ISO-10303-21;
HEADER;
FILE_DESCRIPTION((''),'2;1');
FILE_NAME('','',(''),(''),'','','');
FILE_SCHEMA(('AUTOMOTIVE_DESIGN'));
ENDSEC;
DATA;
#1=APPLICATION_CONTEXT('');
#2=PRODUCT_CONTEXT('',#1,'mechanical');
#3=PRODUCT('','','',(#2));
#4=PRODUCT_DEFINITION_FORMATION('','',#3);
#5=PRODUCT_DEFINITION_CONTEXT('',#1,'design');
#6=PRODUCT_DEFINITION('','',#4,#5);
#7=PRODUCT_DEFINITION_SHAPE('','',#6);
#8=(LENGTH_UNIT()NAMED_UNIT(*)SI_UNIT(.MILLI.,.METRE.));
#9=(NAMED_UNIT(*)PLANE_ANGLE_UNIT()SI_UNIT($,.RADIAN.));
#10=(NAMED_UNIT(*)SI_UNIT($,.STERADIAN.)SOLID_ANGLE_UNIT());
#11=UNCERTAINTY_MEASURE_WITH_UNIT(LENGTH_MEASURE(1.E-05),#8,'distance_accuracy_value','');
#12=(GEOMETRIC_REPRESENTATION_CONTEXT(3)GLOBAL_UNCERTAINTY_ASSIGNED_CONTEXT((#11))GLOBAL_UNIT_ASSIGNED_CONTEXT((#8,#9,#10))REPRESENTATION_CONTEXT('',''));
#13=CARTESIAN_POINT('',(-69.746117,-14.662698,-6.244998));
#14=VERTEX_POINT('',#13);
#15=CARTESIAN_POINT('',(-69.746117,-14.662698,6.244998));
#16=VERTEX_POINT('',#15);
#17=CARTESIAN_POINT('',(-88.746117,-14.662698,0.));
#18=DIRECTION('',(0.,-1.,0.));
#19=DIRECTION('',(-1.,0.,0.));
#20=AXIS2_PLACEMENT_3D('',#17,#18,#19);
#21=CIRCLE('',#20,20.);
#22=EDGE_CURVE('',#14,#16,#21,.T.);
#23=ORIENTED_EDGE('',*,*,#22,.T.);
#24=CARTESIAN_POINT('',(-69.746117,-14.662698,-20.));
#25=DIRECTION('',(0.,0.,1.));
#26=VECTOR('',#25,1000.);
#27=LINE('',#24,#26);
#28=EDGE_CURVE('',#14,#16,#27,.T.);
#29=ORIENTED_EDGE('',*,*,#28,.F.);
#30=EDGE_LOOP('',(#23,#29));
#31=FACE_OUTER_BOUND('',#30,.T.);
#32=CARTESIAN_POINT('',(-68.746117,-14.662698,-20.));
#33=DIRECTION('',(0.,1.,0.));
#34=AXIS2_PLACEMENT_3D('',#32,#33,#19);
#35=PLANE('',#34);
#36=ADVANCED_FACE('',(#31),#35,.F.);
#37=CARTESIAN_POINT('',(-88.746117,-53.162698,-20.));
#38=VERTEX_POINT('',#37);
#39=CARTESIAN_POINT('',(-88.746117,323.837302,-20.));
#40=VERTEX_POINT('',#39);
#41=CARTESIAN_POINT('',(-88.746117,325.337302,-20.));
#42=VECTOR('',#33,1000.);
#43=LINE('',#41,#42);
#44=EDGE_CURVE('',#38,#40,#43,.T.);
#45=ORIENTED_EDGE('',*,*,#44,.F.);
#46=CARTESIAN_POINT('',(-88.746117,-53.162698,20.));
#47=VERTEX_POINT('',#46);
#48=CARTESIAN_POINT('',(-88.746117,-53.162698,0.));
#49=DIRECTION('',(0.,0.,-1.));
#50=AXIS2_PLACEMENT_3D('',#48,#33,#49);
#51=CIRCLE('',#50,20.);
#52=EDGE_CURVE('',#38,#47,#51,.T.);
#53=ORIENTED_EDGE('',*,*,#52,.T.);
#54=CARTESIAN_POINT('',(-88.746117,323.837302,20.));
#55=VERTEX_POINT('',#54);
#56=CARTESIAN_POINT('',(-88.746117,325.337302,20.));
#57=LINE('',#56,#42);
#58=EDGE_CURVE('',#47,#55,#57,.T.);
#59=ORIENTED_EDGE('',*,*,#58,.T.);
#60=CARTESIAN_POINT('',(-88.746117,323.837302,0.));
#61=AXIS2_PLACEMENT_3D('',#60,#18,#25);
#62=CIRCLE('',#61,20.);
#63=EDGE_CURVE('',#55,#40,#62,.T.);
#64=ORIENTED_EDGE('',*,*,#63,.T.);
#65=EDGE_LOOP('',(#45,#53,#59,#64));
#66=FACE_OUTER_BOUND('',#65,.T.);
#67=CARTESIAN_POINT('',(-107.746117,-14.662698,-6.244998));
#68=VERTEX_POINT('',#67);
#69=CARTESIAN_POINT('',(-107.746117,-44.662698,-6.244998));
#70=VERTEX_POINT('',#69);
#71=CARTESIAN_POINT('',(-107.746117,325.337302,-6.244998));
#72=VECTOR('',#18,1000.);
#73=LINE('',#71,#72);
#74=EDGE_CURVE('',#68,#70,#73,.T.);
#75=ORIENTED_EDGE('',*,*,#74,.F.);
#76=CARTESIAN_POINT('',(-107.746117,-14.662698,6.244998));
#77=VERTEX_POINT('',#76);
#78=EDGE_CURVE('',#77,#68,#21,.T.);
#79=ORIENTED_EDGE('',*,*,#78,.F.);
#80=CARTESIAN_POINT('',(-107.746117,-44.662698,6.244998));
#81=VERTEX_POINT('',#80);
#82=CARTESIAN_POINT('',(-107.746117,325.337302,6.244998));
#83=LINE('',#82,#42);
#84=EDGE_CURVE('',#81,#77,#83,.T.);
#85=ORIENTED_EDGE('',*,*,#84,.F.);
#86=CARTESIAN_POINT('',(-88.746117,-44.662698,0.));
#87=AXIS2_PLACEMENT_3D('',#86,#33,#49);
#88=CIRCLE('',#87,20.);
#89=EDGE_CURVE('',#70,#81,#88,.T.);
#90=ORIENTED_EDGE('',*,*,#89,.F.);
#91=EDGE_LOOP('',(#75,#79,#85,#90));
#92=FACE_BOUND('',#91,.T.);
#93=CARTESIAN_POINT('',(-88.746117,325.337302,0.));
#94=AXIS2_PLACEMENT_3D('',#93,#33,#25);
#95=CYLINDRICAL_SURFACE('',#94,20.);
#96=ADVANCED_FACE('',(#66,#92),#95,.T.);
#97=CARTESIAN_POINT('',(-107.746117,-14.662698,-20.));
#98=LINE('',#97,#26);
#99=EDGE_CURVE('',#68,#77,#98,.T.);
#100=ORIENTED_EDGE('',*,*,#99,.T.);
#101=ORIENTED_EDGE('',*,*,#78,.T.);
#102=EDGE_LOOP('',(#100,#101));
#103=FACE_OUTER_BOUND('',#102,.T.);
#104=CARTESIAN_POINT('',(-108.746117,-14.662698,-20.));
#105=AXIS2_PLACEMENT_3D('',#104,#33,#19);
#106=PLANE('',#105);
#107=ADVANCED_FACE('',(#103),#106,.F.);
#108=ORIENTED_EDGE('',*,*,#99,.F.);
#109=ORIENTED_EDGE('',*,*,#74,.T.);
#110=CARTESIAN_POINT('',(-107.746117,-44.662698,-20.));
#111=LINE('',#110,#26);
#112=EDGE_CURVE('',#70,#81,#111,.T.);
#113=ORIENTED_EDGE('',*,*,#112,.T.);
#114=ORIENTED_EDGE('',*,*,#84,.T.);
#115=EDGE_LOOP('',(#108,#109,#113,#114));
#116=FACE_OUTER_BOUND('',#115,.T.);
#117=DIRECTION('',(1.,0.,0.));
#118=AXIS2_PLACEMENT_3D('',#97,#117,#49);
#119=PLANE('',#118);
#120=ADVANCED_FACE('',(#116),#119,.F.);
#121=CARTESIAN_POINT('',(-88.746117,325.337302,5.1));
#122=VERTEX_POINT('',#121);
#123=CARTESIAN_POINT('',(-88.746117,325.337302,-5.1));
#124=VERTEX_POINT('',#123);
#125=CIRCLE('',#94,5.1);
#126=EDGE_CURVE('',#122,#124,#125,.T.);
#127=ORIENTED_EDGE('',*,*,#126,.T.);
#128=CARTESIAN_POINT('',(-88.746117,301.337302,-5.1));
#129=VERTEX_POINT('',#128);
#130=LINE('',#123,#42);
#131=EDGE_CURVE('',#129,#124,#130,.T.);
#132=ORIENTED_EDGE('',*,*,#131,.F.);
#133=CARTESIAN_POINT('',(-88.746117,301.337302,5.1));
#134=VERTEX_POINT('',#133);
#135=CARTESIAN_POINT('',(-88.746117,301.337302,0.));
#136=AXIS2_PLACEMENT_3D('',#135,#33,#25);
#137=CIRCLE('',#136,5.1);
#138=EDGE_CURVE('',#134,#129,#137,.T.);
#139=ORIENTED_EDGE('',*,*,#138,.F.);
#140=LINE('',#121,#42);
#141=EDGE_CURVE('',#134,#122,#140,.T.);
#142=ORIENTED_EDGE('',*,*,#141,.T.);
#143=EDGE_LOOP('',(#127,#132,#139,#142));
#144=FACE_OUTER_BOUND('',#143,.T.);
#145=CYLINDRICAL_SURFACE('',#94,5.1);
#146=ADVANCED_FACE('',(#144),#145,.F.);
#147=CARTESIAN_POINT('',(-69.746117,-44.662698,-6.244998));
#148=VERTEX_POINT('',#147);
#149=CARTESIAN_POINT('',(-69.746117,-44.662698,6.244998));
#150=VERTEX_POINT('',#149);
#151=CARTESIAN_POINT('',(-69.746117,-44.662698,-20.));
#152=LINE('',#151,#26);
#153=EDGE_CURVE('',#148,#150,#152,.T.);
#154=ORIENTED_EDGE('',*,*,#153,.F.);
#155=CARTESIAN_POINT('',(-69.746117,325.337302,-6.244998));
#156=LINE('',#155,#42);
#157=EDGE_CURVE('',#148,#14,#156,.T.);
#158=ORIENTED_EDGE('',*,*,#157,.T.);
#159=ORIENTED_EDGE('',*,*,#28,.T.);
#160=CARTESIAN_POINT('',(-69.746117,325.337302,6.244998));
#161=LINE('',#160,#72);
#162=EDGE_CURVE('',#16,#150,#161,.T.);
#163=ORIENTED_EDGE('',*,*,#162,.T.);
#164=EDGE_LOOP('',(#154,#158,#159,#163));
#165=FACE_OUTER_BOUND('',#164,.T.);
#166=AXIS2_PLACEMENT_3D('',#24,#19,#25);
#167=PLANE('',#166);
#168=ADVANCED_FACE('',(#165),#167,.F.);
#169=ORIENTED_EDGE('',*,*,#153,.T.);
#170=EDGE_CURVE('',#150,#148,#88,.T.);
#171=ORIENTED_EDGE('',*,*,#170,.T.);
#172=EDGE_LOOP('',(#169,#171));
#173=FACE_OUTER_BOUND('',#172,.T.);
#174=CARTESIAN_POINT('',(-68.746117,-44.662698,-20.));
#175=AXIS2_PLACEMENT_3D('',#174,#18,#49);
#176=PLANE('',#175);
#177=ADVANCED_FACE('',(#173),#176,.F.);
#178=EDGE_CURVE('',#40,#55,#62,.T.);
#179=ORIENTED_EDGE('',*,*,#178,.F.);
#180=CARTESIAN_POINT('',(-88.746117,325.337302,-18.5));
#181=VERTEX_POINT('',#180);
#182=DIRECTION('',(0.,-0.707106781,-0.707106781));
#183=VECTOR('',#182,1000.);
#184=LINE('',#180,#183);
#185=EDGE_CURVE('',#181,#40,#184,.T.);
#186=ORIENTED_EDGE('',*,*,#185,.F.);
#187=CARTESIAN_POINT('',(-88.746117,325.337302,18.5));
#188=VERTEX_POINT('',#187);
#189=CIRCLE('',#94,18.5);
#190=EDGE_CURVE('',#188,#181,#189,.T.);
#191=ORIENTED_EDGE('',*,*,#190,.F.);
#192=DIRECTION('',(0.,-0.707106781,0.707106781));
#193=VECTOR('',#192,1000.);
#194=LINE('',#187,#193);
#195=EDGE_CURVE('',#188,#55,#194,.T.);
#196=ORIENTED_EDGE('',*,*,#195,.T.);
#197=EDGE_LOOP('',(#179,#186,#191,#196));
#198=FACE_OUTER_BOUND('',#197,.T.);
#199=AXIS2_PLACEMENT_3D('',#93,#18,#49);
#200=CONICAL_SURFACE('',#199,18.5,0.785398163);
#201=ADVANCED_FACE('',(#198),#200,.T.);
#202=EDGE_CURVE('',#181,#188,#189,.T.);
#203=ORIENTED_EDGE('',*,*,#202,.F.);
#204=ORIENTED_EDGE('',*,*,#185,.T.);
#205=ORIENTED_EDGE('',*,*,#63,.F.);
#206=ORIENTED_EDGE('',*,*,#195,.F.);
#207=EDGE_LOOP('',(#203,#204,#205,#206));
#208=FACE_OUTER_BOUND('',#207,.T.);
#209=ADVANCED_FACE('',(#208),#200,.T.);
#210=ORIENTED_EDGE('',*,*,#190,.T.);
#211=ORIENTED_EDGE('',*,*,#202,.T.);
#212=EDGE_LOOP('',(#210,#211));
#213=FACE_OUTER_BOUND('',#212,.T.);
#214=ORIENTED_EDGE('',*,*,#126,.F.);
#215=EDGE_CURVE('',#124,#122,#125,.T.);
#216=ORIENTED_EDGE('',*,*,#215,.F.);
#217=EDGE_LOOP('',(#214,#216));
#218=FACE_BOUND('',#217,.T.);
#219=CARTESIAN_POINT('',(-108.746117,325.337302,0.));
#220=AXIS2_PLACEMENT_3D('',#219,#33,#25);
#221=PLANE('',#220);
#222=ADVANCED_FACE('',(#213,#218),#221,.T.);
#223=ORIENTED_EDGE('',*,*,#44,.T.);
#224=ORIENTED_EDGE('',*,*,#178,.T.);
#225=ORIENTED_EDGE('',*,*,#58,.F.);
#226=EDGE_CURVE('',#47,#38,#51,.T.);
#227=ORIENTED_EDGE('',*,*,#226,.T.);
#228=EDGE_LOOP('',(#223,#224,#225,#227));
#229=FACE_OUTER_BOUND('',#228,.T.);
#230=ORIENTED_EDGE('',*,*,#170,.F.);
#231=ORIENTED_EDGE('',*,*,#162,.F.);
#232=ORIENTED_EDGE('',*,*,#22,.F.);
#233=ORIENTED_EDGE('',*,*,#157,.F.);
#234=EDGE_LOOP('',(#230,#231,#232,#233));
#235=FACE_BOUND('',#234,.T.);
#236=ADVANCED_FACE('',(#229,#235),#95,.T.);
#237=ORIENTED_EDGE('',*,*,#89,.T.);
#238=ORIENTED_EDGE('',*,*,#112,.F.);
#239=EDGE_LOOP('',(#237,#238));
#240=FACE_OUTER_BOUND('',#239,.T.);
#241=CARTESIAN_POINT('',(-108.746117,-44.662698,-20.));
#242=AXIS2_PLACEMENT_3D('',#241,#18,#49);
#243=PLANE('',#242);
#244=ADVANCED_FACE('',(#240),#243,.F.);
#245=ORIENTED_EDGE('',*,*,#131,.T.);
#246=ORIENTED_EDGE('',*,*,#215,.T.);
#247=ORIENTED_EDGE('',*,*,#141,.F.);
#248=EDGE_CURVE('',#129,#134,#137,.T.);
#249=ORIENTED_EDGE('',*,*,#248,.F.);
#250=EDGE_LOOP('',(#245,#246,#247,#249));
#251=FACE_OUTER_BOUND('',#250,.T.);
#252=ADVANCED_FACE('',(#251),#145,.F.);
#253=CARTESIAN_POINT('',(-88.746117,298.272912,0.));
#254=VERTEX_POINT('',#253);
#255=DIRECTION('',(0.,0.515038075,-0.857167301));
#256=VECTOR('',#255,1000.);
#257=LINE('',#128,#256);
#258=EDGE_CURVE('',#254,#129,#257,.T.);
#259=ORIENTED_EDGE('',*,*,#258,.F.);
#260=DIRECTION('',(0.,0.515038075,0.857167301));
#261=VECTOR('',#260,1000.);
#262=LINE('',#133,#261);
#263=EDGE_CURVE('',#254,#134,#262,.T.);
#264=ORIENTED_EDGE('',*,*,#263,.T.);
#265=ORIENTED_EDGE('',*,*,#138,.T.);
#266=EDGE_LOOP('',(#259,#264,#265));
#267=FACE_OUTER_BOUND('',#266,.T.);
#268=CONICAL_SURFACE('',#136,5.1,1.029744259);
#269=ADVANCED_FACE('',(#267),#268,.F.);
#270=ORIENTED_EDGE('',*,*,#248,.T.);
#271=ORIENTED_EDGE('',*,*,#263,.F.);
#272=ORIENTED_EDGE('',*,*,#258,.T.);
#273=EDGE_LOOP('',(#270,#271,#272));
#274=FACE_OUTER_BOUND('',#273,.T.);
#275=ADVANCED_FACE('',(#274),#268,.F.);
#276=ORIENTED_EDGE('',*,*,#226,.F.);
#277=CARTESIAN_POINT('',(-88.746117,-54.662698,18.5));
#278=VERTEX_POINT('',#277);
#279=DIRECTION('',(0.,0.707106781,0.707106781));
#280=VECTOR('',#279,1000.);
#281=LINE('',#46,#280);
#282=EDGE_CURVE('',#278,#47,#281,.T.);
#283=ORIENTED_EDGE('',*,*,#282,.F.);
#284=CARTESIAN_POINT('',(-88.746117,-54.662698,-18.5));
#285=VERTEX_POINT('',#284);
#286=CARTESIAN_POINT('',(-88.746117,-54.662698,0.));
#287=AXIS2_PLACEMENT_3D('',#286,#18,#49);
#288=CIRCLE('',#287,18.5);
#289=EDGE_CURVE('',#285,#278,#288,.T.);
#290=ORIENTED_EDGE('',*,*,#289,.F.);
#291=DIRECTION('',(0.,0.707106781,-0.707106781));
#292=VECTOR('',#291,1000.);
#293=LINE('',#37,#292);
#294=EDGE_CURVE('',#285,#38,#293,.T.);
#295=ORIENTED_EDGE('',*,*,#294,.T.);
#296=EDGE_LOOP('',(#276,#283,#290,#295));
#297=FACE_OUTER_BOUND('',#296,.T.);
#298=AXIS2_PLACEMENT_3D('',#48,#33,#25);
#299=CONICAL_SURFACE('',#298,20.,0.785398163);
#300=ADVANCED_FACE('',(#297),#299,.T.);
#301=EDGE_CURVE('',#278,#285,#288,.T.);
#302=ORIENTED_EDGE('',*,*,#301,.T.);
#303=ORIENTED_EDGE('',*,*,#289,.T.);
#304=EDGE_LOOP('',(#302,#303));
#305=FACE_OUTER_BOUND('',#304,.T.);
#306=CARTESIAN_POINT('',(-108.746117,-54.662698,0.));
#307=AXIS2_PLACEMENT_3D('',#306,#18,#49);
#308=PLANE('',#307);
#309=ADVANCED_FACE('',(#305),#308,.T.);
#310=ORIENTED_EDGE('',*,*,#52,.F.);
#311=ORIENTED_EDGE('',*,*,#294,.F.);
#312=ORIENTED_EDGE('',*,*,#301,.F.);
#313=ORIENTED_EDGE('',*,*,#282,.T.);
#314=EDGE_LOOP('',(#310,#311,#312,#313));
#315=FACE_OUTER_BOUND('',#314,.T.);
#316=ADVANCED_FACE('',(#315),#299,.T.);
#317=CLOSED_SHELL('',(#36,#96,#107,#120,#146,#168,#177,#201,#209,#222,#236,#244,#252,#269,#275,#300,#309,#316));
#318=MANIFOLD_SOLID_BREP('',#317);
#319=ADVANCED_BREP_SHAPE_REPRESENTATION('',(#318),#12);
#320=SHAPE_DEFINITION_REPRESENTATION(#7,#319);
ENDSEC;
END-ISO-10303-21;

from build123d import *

# Parameters (mm, degrees)
SKETCH1_W               = 20
SKETCH1_H               = 380
CUT_EXTRUDE1_DEPTH      = 344.613267812
CUT_EXTRUDE1_DEPTH_BACK = 344.613267812
SKETCH2_W               = 1
SKETCH2_H               = 30
CHAMFER1_SIZE           = 1.5
M12_TAPPED_HOLE1_D      = 10.2
M12_TAPPED_HOLE1_DEPTH  = 24
M12_TAPPED_HOLE1_TIP    = 3.064389157


with BuildPart() as part:
    # Sketch1 → Revolve1 (revolve)
    with BuildSketch(Plane.XY, mode=Mode.PRIVATE) as revolve1_sk:
        with Locations((-98.74611723, 135.337301587)):
            Rectangle(SKETCH1_W, SKETCH1_H)
    revolve(revolve1_sk.sketch.rotate(Axis((-88.74611723, 325.337301587, 0), (0, -1, 0)), 270), axis=Axis((-88.74611723, 325.337301587, 0), (0, -1, 0)))

    # Sketch2 → Cut-Extrude1 (cut, two sides: drawn at the far end of the back side and taken through both)
    with BuildSketch(Plane.XY.offset(-CUT_EXTRUDE1_DEPTH_BACK)):
        with Locations((-108.24611723, -29.662698413)):
            Rectangle(SKETCH2_W, SKETCH2_H)
        with Locations((-69.24611723, -29.662698413)):
            Rectangle(SKETCH2_W, SKETCH2_H)
    extrude(amount=CUT_EXTRUDE1_DEPTH + CUT_EXTRUDE1_DEPTH_BACK, mode=Mode.SUBTRACT)

    # Chamfer1
    chamfer1_edges = [part.edges().sort_by_distance(p)[0] for p in [
        (-88.74611723, -54.662698413, -20),
        (-88.74611723, 325.337301587, -20),
    ]]
    chamfer(chamfer1_edges, length=CHAMFER1_SIZE)

    # M12 Tapped Hole1
    with Locations(Plane(origin=(0, 325.337301587, 0), x_dir=(1, 0, 0), z_dir=(0, 1, 0))):
        with Locations((-88.74611723, 0)):
            Hole(M12_TAPPED_HOLE1_D / 2, depth=M12_TAPPED_HOLE1_DEPTH)
            with Locations((0, 0, -(M12_TAPPED_HOLE1_DEPTH + M12_TAPPED_HOLE1_TIP / 2))):  # 118° drill point
                Cone(0, M12_TAPPED_HOLE1_D / 2, M12_TAPPED_HOLE1_TIP, mode=Mode.SUBTRACT)


solid = part.part
